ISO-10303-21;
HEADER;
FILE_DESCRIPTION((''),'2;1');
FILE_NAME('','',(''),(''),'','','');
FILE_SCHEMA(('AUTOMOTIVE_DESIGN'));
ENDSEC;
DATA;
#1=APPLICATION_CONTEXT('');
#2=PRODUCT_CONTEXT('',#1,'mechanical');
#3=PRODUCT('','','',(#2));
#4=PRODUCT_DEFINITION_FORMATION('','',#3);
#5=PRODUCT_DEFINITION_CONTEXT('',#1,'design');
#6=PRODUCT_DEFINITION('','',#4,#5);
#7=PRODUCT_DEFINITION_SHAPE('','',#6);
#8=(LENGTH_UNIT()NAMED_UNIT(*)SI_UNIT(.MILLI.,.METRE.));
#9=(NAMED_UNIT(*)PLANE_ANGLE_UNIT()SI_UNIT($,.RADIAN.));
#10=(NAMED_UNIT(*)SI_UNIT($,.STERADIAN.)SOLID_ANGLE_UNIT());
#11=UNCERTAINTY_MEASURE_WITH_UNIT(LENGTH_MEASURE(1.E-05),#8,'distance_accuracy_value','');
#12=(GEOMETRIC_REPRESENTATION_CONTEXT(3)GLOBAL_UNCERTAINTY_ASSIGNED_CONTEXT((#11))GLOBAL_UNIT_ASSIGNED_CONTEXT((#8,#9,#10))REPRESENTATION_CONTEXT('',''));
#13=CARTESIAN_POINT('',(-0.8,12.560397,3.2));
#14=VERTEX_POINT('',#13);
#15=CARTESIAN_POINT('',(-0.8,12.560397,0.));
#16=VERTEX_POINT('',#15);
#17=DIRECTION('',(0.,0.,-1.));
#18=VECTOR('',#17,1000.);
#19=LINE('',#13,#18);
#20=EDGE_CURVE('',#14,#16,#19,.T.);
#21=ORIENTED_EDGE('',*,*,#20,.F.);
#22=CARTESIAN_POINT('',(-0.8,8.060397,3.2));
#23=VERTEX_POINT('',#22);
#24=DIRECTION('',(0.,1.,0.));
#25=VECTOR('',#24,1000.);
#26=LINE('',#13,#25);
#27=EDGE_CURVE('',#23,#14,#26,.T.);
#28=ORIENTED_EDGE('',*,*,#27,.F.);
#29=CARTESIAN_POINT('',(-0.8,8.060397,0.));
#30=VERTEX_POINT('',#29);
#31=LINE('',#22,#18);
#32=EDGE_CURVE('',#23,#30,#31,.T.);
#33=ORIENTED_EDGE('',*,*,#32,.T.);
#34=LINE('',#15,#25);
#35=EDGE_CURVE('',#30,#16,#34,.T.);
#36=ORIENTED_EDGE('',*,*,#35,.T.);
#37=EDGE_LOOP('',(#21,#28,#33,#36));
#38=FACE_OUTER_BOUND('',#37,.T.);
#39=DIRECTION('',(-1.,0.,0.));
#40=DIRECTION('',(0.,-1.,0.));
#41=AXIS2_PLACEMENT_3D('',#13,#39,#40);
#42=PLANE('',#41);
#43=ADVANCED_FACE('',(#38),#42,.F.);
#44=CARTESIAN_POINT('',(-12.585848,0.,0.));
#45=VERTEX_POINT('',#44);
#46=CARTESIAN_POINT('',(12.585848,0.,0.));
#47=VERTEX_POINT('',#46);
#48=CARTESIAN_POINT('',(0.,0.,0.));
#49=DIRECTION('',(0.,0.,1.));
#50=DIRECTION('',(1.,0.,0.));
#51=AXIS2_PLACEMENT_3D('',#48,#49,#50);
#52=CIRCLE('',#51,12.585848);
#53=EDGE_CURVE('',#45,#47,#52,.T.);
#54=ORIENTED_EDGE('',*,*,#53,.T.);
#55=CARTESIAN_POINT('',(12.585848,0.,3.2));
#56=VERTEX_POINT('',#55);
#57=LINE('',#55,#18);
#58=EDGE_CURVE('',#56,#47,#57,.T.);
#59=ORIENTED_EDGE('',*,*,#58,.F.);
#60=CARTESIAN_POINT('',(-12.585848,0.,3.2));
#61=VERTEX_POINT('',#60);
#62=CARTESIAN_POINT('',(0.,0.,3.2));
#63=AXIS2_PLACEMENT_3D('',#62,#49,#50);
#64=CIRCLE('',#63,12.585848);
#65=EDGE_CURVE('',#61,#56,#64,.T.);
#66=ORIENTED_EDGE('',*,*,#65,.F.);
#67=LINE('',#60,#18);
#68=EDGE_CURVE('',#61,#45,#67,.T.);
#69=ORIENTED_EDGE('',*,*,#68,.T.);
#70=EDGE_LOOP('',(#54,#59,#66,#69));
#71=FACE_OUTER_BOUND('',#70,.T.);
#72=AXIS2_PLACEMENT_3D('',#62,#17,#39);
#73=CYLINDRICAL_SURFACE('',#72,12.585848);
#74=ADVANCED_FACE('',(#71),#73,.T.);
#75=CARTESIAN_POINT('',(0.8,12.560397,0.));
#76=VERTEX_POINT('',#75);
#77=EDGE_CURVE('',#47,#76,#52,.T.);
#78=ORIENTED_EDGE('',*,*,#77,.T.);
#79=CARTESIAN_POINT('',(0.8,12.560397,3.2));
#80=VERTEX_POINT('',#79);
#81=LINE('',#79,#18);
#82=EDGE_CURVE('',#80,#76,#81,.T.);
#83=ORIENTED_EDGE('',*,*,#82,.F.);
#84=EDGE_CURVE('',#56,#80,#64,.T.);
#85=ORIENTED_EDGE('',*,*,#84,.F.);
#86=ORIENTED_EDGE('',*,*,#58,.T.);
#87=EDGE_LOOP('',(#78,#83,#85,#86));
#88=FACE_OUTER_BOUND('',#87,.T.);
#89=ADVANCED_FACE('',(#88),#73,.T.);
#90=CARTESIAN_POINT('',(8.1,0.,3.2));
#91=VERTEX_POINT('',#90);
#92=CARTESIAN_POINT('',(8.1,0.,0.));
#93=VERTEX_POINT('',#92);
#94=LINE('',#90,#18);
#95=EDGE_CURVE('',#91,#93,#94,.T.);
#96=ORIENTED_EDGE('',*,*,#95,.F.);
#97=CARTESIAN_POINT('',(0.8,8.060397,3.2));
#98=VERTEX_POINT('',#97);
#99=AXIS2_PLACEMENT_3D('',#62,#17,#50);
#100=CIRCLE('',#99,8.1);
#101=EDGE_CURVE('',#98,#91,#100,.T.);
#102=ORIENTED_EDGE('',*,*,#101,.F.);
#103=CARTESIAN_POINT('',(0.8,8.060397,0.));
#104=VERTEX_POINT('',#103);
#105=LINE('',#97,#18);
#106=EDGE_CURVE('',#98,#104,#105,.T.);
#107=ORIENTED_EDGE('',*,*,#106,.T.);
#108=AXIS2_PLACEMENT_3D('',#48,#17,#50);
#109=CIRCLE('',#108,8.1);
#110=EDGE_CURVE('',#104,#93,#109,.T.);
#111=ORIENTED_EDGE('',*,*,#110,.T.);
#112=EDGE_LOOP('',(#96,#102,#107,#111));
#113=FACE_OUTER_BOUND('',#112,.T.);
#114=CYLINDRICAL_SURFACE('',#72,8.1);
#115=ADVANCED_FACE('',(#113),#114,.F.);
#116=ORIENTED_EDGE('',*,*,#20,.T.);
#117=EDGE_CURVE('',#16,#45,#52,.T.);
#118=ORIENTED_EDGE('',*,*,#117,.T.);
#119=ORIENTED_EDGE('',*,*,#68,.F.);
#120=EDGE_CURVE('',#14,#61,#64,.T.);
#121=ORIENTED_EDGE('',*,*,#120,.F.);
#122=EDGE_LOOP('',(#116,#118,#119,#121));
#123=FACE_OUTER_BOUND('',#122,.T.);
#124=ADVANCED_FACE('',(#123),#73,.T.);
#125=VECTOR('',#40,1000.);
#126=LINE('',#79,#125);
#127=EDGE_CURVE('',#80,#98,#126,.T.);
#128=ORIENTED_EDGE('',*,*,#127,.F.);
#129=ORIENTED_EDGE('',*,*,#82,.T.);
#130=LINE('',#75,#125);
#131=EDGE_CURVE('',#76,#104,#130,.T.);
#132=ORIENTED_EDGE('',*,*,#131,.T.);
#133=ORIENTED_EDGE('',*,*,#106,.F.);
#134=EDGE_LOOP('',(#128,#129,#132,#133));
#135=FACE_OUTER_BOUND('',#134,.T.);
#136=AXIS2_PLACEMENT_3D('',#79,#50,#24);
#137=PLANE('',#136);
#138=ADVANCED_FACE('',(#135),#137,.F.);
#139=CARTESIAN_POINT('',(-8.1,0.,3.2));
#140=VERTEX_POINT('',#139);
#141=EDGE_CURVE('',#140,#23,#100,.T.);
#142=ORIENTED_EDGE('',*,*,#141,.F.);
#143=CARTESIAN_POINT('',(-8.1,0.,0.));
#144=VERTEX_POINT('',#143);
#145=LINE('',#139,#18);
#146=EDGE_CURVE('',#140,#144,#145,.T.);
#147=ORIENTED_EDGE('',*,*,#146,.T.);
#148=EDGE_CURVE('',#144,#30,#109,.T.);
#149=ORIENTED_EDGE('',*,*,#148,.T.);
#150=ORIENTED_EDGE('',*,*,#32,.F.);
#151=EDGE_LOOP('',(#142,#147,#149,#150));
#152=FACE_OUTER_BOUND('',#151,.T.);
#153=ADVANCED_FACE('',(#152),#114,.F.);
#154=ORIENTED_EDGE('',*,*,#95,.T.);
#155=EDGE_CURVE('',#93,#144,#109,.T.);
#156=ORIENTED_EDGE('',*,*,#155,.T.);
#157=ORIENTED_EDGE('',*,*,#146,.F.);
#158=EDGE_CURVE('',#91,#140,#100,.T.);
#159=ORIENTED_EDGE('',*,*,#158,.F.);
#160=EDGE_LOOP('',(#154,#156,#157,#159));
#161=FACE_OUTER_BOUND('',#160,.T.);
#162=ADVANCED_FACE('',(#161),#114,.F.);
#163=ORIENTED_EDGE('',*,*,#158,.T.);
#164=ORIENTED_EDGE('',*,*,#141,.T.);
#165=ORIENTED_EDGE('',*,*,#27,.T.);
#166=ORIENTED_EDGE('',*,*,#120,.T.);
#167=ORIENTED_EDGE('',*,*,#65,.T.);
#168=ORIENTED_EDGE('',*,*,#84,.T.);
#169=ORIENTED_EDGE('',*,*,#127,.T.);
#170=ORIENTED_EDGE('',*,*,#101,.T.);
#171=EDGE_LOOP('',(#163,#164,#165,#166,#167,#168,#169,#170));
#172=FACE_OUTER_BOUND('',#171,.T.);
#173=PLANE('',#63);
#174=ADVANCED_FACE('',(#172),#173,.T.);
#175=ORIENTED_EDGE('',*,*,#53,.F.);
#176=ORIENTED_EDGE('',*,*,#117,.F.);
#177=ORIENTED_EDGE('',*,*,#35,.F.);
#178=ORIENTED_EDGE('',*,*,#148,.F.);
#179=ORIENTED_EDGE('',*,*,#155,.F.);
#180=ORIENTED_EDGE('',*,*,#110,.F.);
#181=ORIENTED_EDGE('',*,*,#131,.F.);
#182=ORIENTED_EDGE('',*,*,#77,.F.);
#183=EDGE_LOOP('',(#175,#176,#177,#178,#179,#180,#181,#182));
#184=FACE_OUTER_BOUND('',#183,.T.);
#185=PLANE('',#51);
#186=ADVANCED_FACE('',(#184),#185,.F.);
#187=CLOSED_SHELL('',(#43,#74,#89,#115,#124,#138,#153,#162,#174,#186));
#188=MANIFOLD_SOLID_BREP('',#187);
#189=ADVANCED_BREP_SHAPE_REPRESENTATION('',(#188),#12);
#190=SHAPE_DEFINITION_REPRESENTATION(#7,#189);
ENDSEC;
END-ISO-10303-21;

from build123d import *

# Parameters (mm, degrees)
EXTRUDE_1_DEPTH = 3.2


with BuildPart() as part:
    # Sketch 263 → 拉伸1 (new body)
    with BuildSketch(Plane.XY):
        with BuildLine():
            Line((-0.8, 12.560397013), (-0.8, 8.060397013))
            ThreePointArc((-0.8, 8.060397013), (0, -8.1), (0.8, 8.060397013))
            Line((0.8, 8.060397013), (0.8, 12.560397013))
            ThreePointArc((0.8, 12.560397013), (0, -12.585848128), (-0.8, 12.560397013))
        make_face()
    extrude(amount=EXTRUDE_1_DEPTH)


solid = part.part
